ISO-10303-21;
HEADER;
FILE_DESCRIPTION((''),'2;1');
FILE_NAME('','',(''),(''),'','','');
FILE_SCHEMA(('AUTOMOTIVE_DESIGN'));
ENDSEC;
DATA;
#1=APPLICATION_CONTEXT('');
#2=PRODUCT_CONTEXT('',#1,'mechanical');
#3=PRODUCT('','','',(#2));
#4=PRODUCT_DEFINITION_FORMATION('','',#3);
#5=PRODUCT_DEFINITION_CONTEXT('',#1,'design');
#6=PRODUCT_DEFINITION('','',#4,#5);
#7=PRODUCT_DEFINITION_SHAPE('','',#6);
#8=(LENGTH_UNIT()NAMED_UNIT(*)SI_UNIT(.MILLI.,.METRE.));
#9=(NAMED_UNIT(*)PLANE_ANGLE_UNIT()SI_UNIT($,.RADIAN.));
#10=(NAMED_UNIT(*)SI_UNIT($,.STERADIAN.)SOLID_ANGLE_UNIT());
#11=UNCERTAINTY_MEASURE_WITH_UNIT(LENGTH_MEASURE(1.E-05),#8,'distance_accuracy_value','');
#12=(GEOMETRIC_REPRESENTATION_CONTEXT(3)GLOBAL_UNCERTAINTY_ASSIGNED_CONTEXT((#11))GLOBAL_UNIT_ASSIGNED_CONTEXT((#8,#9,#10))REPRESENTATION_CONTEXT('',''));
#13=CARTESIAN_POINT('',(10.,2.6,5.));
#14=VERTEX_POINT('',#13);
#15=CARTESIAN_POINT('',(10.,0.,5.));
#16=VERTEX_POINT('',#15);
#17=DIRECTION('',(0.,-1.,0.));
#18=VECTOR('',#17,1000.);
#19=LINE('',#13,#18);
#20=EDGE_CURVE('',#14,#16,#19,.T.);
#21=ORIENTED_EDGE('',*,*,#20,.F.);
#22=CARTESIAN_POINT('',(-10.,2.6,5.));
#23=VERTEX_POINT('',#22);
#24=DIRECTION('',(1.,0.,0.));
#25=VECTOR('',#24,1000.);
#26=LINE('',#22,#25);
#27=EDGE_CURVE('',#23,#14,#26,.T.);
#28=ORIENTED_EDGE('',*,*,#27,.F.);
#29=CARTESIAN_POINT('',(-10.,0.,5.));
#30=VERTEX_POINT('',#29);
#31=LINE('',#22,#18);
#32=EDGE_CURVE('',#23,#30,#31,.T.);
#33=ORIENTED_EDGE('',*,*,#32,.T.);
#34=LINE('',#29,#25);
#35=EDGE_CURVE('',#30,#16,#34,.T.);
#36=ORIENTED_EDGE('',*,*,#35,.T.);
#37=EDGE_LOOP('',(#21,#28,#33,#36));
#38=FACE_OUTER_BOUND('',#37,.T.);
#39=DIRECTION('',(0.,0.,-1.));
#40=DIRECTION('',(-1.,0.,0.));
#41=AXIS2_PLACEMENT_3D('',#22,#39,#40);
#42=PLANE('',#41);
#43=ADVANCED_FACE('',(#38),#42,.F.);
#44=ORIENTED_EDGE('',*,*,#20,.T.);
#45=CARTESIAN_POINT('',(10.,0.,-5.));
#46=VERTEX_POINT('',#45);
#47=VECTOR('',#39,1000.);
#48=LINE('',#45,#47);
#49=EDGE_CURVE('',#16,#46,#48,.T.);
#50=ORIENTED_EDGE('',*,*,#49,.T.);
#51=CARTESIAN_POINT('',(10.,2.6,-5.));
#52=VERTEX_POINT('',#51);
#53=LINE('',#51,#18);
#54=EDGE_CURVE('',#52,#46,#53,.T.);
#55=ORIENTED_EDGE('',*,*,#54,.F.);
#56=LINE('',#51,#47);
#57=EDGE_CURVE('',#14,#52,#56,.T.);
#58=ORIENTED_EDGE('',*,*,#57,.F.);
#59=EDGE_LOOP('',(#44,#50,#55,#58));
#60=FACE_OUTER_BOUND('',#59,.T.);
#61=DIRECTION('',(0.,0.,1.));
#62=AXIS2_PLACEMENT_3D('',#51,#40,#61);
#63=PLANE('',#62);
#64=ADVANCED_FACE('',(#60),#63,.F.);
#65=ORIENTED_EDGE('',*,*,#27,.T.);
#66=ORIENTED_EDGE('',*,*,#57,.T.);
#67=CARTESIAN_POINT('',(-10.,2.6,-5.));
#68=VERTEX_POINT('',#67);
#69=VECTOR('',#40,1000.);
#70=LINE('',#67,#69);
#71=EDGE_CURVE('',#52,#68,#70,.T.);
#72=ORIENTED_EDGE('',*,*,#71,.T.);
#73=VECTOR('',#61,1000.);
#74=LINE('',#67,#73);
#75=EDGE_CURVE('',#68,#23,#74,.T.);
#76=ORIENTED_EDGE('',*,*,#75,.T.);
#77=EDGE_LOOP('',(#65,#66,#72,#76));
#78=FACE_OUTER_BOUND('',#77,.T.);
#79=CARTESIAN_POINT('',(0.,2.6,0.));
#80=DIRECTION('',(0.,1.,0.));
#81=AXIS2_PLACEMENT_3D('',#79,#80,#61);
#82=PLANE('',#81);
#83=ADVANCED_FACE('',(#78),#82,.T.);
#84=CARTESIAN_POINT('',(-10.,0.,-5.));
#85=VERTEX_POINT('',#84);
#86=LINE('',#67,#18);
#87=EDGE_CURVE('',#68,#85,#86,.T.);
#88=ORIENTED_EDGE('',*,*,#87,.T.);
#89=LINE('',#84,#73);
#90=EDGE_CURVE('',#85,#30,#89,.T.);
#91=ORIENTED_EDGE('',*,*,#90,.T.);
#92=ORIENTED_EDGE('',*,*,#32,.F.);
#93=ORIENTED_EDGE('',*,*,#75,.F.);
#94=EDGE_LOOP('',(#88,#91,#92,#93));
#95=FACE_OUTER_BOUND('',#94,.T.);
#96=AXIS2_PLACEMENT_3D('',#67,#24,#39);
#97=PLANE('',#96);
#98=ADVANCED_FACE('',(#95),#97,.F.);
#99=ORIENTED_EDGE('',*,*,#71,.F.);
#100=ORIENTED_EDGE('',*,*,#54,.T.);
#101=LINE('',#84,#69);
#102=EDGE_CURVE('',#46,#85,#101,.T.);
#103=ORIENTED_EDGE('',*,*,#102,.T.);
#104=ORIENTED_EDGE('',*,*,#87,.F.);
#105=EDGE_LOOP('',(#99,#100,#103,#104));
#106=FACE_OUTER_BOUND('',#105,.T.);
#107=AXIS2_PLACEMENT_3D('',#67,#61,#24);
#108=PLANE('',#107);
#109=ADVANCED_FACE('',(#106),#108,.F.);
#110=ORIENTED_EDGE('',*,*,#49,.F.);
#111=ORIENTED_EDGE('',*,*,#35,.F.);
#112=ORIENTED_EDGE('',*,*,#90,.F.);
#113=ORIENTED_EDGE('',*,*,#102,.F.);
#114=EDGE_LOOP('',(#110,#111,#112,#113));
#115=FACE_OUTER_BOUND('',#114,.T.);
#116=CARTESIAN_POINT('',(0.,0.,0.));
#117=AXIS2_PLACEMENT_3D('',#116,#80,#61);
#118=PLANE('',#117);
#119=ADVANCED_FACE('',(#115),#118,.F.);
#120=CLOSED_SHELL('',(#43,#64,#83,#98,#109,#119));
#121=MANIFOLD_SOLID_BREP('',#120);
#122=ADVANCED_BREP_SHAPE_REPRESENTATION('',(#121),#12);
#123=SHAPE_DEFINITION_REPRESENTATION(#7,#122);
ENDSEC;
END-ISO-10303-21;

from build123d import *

# Parameters (mm, degrees)
SKETCH1_W           = 20
SKETCH1_H           = 10
BOSS_EXTRUDE1_DEPTH = 2.6


with BuildPart() as part:
    # Sketch1 → Boss-Extrude1 (new body)
    with BuildSketch(Plane(origin=(0, 0, 0), x_dir=(1, 0, 0), z_dir=(0, 1, 0))):
        Rectangle(SKETCH1_W, SKETCH1_H)
    extrude(amount=BOSS_EXTRUDE1_DEPTH)


solid = part.part
